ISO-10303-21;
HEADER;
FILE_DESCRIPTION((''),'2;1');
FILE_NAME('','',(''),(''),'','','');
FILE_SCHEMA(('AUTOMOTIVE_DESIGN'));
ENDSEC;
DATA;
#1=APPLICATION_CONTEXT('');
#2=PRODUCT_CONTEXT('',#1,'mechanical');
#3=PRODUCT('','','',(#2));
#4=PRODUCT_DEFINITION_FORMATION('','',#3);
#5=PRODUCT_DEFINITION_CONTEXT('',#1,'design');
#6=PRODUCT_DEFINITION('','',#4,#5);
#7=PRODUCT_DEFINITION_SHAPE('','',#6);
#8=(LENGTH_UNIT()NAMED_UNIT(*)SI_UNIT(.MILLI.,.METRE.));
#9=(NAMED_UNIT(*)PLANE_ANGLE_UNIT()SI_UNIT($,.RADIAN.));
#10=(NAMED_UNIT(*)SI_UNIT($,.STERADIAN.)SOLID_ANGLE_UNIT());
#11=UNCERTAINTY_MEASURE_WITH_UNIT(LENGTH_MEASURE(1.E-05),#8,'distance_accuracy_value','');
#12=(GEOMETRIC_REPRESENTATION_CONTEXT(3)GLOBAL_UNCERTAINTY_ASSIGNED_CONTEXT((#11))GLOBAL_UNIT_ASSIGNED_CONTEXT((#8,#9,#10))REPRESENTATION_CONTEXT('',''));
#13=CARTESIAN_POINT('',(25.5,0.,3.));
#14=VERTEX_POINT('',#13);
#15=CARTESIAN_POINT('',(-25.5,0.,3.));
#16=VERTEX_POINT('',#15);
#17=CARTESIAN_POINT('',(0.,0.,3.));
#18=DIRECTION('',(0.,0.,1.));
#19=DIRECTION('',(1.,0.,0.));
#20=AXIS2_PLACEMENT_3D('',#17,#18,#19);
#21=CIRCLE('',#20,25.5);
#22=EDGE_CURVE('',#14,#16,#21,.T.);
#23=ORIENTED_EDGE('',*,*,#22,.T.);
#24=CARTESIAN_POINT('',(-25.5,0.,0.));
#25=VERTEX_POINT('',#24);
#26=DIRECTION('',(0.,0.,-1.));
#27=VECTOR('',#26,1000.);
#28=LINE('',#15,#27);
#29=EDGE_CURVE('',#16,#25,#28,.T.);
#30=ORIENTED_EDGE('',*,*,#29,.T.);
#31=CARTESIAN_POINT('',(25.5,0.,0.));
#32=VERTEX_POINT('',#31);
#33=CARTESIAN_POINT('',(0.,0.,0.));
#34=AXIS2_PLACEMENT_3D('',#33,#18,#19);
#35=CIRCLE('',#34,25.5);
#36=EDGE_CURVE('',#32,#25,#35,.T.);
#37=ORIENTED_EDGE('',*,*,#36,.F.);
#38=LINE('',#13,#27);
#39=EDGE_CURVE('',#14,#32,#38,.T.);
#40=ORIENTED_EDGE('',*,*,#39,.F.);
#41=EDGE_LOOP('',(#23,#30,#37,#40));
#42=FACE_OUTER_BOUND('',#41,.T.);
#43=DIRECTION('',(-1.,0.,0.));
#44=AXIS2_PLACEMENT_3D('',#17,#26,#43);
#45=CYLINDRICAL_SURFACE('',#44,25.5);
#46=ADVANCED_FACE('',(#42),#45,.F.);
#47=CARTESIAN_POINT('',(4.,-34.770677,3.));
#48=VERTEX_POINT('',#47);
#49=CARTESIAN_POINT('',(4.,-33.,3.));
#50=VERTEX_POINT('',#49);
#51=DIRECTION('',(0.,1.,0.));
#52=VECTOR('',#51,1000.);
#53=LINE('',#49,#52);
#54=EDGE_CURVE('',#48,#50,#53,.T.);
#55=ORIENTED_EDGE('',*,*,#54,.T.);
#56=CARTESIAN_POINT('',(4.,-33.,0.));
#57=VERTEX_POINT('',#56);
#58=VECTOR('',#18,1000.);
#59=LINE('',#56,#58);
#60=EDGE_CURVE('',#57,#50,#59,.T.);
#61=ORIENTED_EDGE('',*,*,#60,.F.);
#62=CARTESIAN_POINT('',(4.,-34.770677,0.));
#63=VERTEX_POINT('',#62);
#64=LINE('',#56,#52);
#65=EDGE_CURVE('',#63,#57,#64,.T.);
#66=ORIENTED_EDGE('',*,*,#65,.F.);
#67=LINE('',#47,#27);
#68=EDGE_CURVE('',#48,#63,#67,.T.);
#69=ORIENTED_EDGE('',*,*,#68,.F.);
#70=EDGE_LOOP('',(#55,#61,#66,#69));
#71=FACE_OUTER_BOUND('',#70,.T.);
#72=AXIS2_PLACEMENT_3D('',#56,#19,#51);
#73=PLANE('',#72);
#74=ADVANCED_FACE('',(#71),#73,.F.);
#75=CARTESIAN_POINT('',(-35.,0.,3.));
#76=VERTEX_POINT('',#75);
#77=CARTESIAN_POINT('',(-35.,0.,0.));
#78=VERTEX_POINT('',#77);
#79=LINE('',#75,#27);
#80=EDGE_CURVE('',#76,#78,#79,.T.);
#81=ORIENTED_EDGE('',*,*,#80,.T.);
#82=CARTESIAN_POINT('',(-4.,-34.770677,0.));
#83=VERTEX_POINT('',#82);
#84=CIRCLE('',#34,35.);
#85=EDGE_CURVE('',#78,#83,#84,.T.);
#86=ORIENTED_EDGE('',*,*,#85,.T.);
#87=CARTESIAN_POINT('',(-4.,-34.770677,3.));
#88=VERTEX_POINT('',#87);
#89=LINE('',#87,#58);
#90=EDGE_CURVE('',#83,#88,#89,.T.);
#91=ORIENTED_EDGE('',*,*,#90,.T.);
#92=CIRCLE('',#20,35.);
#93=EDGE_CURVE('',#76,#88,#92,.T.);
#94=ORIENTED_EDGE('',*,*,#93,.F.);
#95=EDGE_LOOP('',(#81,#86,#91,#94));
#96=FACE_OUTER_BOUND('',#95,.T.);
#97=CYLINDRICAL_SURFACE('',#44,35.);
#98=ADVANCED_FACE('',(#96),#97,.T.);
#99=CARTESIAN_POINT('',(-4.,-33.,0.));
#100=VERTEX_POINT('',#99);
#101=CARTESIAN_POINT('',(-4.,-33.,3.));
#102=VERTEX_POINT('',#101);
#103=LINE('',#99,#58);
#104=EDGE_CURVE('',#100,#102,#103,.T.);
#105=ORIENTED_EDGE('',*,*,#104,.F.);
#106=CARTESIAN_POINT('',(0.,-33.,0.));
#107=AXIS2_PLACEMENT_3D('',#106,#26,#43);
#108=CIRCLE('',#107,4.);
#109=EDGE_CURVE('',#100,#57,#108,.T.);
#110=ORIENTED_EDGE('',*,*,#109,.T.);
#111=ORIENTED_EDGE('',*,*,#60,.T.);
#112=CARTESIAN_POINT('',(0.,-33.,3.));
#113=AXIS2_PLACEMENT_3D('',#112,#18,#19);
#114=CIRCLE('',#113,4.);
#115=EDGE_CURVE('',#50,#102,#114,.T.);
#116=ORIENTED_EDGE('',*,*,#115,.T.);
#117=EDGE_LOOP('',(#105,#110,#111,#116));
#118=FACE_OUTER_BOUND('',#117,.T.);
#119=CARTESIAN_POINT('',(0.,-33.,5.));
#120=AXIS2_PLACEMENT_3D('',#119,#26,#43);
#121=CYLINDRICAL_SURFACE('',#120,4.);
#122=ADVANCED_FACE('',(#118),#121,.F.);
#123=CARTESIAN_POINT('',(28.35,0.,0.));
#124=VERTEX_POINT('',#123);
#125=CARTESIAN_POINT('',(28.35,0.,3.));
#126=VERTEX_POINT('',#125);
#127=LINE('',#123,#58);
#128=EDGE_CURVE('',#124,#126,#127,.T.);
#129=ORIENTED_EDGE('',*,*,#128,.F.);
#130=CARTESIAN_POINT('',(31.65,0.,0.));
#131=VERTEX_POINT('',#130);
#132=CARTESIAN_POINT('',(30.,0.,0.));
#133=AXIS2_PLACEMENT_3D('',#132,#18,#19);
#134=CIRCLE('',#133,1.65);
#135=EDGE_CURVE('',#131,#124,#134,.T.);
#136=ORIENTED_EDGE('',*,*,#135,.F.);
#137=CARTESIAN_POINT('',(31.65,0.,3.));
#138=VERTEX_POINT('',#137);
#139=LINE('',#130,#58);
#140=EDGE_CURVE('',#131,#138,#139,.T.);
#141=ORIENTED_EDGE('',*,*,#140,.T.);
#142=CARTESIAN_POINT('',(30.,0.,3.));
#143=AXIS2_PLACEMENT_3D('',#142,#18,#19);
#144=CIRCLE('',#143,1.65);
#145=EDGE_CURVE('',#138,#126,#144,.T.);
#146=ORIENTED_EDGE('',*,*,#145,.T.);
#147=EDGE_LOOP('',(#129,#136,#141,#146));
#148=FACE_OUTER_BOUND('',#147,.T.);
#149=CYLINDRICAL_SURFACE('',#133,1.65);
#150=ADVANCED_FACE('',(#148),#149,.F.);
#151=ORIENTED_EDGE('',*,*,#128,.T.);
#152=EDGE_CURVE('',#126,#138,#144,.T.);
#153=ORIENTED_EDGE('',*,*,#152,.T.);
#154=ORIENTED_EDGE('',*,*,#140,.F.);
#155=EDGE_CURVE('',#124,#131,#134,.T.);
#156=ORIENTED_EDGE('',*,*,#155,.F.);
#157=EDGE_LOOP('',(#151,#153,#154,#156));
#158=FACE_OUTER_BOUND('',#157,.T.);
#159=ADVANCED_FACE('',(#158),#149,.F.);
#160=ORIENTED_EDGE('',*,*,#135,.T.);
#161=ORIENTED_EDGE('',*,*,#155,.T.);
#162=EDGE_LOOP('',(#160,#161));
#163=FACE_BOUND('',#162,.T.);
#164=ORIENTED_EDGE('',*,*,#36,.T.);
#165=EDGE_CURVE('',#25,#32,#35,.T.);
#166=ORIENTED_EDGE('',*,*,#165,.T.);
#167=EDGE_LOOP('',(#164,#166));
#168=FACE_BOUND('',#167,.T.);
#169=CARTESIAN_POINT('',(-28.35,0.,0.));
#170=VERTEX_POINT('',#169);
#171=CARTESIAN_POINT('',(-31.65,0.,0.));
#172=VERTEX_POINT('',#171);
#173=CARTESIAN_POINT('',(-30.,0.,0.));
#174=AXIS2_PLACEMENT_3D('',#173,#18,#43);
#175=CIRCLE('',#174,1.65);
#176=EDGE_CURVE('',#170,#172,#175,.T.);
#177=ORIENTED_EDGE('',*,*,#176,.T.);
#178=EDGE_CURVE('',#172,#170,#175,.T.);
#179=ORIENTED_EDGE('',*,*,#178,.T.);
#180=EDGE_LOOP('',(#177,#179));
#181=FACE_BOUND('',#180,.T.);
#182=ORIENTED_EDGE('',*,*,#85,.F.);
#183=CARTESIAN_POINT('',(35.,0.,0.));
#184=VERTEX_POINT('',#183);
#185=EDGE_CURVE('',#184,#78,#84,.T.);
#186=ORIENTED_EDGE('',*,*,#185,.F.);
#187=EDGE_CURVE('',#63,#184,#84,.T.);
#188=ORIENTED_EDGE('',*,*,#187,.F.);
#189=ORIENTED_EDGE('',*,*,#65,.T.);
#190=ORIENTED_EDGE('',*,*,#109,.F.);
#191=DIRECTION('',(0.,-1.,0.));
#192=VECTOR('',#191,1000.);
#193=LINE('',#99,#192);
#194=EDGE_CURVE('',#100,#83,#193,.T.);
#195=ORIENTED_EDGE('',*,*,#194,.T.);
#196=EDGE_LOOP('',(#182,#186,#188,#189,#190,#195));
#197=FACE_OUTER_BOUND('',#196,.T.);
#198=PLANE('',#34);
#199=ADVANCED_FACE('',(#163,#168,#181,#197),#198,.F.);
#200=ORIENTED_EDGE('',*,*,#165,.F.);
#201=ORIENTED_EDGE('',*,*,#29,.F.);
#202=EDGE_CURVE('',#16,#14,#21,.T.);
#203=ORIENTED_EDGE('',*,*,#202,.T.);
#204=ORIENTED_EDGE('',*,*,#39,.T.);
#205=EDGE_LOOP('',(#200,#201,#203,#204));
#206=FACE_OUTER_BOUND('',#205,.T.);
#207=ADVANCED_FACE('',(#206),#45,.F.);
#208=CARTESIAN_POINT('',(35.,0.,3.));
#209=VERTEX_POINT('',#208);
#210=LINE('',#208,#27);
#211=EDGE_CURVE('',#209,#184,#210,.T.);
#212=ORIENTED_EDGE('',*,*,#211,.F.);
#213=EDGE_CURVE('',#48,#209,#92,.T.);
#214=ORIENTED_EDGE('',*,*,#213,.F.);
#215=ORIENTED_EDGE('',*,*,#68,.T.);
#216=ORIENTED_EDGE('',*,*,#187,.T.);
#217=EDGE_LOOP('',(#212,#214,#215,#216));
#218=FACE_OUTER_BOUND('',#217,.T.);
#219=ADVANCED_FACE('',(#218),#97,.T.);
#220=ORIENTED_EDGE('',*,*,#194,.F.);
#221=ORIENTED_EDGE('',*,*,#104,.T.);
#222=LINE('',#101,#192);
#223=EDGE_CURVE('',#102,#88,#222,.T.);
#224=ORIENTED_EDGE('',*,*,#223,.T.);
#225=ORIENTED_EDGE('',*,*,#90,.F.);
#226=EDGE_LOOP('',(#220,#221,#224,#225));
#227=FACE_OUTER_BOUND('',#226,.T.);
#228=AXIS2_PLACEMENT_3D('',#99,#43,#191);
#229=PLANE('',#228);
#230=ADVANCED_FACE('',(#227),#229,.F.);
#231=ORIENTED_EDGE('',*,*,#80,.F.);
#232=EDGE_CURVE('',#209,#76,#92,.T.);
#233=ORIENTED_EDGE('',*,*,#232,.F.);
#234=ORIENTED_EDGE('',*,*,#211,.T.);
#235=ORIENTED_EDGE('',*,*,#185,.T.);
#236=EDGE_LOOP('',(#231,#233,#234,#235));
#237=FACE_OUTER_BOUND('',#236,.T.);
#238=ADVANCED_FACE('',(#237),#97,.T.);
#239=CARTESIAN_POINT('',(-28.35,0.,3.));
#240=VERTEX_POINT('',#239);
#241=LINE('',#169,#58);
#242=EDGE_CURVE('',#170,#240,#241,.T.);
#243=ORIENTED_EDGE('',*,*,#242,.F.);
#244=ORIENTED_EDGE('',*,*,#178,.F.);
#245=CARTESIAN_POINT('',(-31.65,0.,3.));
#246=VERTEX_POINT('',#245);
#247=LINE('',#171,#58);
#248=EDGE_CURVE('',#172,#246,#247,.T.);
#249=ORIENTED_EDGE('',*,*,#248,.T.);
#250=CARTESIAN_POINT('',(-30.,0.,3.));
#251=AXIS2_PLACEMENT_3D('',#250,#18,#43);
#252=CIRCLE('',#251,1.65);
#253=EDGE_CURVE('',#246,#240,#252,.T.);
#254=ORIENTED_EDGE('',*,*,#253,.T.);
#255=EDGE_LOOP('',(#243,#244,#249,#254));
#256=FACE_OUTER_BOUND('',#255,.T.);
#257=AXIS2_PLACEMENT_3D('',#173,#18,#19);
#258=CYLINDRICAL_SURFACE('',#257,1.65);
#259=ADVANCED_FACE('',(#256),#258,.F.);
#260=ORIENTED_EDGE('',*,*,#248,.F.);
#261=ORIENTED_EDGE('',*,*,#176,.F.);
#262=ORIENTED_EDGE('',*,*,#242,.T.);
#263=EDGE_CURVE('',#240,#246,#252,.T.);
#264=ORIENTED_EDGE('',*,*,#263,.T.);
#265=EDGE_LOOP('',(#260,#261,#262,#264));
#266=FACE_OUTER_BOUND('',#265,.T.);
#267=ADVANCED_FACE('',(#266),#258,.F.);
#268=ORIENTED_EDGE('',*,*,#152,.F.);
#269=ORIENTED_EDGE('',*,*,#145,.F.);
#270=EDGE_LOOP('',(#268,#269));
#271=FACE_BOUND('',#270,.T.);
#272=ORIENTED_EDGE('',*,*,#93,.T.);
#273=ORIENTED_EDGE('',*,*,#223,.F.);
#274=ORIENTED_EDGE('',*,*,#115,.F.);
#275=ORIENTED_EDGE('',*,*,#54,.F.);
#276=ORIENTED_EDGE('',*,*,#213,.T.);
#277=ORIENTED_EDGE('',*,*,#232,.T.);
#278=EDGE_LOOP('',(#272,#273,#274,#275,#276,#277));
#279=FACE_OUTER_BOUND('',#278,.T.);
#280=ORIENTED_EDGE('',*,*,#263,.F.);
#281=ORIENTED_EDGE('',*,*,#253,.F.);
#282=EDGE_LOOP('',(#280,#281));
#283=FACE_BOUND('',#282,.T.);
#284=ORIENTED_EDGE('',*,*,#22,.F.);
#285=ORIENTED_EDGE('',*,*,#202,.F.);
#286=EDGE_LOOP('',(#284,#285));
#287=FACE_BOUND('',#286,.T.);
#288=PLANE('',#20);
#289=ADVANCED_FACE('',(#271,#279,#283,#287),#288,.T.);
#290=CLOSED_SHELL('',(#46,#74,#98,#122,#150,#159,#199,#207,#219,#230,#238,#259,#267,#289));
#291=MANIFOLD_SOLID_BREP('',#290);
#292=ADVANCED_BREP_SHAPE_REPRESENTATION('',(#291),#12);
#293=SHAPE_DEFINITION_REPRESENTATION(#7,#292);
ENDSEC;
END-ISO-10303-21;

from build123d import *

# Parameters (mm, degrees)
SKETCH2_R           = 35
SKETCH2_R_2         = 25.5
BOSS_EXTRUDE1_DEPTH = 3
SKETCH3_R           = 4
CUT_EXTRUDE1_DEPTH  = 5
SKETCH8_W           = 8
SKETCH8_H           = 8.160533217
CUT_EXTRUDE3_DEPTH  = 50.588305073
SKETCH9_R           = 1.65
CUT_EXTRUDE4_DEPTH  = 50.588305073


with BuildPart() as part:
    # Sketch2 → Boss-Extrude1 (new body)
    with BuildSketch(Plane.XY):
        Circle(SKETCH2_R)
        Circle(SKETCH2_R_2, mode=Mode.SUBTRACT)
    extrude(amount=BOSS_EXTRUDE1_DEPTH)

    # Sketch3 → Cut-Extrude1 (cut)
    with BuildSketch(Plane(origin=(0, 0, 0), x_dir=(-1, 0, 0), z_dir=(0, 0, -1))):
        with Locations((0, -33)):
            Circle(SKETCH3_R)
    extrude(amount=-CUT_EXTRUDE1_DEPTH, mode=Mode.SUBTRACT)

    # Sketch8 → Cut-Extrude3 (cut, through all)
    with BuildSketch(Plane.XY.offset(3)):
        with Locations((0, -37.080266608)):
            Rectangle(SKETCH8_W, SKETCH8_H)
    extrude(amount=-CUT_EXTRUDE3_DEPTH, mode=Mode.SUBTRACT)

    # Sketch9 → Cut-Extrude4 (cut, through all)
    with BuildSketch(Plane.XY.offset(3)):
        with Locations((30, 0)):
            Circle(SKETCH9_R)
        with Locations(Location((-30, 0, 0), (0, 0, 180))):
            Circle(SKETCH9_R)
    extrude(amount=-CUT_EXTRUDE4_DEPTH, mode=Mode.SUBTRACT)


solid = part.part
